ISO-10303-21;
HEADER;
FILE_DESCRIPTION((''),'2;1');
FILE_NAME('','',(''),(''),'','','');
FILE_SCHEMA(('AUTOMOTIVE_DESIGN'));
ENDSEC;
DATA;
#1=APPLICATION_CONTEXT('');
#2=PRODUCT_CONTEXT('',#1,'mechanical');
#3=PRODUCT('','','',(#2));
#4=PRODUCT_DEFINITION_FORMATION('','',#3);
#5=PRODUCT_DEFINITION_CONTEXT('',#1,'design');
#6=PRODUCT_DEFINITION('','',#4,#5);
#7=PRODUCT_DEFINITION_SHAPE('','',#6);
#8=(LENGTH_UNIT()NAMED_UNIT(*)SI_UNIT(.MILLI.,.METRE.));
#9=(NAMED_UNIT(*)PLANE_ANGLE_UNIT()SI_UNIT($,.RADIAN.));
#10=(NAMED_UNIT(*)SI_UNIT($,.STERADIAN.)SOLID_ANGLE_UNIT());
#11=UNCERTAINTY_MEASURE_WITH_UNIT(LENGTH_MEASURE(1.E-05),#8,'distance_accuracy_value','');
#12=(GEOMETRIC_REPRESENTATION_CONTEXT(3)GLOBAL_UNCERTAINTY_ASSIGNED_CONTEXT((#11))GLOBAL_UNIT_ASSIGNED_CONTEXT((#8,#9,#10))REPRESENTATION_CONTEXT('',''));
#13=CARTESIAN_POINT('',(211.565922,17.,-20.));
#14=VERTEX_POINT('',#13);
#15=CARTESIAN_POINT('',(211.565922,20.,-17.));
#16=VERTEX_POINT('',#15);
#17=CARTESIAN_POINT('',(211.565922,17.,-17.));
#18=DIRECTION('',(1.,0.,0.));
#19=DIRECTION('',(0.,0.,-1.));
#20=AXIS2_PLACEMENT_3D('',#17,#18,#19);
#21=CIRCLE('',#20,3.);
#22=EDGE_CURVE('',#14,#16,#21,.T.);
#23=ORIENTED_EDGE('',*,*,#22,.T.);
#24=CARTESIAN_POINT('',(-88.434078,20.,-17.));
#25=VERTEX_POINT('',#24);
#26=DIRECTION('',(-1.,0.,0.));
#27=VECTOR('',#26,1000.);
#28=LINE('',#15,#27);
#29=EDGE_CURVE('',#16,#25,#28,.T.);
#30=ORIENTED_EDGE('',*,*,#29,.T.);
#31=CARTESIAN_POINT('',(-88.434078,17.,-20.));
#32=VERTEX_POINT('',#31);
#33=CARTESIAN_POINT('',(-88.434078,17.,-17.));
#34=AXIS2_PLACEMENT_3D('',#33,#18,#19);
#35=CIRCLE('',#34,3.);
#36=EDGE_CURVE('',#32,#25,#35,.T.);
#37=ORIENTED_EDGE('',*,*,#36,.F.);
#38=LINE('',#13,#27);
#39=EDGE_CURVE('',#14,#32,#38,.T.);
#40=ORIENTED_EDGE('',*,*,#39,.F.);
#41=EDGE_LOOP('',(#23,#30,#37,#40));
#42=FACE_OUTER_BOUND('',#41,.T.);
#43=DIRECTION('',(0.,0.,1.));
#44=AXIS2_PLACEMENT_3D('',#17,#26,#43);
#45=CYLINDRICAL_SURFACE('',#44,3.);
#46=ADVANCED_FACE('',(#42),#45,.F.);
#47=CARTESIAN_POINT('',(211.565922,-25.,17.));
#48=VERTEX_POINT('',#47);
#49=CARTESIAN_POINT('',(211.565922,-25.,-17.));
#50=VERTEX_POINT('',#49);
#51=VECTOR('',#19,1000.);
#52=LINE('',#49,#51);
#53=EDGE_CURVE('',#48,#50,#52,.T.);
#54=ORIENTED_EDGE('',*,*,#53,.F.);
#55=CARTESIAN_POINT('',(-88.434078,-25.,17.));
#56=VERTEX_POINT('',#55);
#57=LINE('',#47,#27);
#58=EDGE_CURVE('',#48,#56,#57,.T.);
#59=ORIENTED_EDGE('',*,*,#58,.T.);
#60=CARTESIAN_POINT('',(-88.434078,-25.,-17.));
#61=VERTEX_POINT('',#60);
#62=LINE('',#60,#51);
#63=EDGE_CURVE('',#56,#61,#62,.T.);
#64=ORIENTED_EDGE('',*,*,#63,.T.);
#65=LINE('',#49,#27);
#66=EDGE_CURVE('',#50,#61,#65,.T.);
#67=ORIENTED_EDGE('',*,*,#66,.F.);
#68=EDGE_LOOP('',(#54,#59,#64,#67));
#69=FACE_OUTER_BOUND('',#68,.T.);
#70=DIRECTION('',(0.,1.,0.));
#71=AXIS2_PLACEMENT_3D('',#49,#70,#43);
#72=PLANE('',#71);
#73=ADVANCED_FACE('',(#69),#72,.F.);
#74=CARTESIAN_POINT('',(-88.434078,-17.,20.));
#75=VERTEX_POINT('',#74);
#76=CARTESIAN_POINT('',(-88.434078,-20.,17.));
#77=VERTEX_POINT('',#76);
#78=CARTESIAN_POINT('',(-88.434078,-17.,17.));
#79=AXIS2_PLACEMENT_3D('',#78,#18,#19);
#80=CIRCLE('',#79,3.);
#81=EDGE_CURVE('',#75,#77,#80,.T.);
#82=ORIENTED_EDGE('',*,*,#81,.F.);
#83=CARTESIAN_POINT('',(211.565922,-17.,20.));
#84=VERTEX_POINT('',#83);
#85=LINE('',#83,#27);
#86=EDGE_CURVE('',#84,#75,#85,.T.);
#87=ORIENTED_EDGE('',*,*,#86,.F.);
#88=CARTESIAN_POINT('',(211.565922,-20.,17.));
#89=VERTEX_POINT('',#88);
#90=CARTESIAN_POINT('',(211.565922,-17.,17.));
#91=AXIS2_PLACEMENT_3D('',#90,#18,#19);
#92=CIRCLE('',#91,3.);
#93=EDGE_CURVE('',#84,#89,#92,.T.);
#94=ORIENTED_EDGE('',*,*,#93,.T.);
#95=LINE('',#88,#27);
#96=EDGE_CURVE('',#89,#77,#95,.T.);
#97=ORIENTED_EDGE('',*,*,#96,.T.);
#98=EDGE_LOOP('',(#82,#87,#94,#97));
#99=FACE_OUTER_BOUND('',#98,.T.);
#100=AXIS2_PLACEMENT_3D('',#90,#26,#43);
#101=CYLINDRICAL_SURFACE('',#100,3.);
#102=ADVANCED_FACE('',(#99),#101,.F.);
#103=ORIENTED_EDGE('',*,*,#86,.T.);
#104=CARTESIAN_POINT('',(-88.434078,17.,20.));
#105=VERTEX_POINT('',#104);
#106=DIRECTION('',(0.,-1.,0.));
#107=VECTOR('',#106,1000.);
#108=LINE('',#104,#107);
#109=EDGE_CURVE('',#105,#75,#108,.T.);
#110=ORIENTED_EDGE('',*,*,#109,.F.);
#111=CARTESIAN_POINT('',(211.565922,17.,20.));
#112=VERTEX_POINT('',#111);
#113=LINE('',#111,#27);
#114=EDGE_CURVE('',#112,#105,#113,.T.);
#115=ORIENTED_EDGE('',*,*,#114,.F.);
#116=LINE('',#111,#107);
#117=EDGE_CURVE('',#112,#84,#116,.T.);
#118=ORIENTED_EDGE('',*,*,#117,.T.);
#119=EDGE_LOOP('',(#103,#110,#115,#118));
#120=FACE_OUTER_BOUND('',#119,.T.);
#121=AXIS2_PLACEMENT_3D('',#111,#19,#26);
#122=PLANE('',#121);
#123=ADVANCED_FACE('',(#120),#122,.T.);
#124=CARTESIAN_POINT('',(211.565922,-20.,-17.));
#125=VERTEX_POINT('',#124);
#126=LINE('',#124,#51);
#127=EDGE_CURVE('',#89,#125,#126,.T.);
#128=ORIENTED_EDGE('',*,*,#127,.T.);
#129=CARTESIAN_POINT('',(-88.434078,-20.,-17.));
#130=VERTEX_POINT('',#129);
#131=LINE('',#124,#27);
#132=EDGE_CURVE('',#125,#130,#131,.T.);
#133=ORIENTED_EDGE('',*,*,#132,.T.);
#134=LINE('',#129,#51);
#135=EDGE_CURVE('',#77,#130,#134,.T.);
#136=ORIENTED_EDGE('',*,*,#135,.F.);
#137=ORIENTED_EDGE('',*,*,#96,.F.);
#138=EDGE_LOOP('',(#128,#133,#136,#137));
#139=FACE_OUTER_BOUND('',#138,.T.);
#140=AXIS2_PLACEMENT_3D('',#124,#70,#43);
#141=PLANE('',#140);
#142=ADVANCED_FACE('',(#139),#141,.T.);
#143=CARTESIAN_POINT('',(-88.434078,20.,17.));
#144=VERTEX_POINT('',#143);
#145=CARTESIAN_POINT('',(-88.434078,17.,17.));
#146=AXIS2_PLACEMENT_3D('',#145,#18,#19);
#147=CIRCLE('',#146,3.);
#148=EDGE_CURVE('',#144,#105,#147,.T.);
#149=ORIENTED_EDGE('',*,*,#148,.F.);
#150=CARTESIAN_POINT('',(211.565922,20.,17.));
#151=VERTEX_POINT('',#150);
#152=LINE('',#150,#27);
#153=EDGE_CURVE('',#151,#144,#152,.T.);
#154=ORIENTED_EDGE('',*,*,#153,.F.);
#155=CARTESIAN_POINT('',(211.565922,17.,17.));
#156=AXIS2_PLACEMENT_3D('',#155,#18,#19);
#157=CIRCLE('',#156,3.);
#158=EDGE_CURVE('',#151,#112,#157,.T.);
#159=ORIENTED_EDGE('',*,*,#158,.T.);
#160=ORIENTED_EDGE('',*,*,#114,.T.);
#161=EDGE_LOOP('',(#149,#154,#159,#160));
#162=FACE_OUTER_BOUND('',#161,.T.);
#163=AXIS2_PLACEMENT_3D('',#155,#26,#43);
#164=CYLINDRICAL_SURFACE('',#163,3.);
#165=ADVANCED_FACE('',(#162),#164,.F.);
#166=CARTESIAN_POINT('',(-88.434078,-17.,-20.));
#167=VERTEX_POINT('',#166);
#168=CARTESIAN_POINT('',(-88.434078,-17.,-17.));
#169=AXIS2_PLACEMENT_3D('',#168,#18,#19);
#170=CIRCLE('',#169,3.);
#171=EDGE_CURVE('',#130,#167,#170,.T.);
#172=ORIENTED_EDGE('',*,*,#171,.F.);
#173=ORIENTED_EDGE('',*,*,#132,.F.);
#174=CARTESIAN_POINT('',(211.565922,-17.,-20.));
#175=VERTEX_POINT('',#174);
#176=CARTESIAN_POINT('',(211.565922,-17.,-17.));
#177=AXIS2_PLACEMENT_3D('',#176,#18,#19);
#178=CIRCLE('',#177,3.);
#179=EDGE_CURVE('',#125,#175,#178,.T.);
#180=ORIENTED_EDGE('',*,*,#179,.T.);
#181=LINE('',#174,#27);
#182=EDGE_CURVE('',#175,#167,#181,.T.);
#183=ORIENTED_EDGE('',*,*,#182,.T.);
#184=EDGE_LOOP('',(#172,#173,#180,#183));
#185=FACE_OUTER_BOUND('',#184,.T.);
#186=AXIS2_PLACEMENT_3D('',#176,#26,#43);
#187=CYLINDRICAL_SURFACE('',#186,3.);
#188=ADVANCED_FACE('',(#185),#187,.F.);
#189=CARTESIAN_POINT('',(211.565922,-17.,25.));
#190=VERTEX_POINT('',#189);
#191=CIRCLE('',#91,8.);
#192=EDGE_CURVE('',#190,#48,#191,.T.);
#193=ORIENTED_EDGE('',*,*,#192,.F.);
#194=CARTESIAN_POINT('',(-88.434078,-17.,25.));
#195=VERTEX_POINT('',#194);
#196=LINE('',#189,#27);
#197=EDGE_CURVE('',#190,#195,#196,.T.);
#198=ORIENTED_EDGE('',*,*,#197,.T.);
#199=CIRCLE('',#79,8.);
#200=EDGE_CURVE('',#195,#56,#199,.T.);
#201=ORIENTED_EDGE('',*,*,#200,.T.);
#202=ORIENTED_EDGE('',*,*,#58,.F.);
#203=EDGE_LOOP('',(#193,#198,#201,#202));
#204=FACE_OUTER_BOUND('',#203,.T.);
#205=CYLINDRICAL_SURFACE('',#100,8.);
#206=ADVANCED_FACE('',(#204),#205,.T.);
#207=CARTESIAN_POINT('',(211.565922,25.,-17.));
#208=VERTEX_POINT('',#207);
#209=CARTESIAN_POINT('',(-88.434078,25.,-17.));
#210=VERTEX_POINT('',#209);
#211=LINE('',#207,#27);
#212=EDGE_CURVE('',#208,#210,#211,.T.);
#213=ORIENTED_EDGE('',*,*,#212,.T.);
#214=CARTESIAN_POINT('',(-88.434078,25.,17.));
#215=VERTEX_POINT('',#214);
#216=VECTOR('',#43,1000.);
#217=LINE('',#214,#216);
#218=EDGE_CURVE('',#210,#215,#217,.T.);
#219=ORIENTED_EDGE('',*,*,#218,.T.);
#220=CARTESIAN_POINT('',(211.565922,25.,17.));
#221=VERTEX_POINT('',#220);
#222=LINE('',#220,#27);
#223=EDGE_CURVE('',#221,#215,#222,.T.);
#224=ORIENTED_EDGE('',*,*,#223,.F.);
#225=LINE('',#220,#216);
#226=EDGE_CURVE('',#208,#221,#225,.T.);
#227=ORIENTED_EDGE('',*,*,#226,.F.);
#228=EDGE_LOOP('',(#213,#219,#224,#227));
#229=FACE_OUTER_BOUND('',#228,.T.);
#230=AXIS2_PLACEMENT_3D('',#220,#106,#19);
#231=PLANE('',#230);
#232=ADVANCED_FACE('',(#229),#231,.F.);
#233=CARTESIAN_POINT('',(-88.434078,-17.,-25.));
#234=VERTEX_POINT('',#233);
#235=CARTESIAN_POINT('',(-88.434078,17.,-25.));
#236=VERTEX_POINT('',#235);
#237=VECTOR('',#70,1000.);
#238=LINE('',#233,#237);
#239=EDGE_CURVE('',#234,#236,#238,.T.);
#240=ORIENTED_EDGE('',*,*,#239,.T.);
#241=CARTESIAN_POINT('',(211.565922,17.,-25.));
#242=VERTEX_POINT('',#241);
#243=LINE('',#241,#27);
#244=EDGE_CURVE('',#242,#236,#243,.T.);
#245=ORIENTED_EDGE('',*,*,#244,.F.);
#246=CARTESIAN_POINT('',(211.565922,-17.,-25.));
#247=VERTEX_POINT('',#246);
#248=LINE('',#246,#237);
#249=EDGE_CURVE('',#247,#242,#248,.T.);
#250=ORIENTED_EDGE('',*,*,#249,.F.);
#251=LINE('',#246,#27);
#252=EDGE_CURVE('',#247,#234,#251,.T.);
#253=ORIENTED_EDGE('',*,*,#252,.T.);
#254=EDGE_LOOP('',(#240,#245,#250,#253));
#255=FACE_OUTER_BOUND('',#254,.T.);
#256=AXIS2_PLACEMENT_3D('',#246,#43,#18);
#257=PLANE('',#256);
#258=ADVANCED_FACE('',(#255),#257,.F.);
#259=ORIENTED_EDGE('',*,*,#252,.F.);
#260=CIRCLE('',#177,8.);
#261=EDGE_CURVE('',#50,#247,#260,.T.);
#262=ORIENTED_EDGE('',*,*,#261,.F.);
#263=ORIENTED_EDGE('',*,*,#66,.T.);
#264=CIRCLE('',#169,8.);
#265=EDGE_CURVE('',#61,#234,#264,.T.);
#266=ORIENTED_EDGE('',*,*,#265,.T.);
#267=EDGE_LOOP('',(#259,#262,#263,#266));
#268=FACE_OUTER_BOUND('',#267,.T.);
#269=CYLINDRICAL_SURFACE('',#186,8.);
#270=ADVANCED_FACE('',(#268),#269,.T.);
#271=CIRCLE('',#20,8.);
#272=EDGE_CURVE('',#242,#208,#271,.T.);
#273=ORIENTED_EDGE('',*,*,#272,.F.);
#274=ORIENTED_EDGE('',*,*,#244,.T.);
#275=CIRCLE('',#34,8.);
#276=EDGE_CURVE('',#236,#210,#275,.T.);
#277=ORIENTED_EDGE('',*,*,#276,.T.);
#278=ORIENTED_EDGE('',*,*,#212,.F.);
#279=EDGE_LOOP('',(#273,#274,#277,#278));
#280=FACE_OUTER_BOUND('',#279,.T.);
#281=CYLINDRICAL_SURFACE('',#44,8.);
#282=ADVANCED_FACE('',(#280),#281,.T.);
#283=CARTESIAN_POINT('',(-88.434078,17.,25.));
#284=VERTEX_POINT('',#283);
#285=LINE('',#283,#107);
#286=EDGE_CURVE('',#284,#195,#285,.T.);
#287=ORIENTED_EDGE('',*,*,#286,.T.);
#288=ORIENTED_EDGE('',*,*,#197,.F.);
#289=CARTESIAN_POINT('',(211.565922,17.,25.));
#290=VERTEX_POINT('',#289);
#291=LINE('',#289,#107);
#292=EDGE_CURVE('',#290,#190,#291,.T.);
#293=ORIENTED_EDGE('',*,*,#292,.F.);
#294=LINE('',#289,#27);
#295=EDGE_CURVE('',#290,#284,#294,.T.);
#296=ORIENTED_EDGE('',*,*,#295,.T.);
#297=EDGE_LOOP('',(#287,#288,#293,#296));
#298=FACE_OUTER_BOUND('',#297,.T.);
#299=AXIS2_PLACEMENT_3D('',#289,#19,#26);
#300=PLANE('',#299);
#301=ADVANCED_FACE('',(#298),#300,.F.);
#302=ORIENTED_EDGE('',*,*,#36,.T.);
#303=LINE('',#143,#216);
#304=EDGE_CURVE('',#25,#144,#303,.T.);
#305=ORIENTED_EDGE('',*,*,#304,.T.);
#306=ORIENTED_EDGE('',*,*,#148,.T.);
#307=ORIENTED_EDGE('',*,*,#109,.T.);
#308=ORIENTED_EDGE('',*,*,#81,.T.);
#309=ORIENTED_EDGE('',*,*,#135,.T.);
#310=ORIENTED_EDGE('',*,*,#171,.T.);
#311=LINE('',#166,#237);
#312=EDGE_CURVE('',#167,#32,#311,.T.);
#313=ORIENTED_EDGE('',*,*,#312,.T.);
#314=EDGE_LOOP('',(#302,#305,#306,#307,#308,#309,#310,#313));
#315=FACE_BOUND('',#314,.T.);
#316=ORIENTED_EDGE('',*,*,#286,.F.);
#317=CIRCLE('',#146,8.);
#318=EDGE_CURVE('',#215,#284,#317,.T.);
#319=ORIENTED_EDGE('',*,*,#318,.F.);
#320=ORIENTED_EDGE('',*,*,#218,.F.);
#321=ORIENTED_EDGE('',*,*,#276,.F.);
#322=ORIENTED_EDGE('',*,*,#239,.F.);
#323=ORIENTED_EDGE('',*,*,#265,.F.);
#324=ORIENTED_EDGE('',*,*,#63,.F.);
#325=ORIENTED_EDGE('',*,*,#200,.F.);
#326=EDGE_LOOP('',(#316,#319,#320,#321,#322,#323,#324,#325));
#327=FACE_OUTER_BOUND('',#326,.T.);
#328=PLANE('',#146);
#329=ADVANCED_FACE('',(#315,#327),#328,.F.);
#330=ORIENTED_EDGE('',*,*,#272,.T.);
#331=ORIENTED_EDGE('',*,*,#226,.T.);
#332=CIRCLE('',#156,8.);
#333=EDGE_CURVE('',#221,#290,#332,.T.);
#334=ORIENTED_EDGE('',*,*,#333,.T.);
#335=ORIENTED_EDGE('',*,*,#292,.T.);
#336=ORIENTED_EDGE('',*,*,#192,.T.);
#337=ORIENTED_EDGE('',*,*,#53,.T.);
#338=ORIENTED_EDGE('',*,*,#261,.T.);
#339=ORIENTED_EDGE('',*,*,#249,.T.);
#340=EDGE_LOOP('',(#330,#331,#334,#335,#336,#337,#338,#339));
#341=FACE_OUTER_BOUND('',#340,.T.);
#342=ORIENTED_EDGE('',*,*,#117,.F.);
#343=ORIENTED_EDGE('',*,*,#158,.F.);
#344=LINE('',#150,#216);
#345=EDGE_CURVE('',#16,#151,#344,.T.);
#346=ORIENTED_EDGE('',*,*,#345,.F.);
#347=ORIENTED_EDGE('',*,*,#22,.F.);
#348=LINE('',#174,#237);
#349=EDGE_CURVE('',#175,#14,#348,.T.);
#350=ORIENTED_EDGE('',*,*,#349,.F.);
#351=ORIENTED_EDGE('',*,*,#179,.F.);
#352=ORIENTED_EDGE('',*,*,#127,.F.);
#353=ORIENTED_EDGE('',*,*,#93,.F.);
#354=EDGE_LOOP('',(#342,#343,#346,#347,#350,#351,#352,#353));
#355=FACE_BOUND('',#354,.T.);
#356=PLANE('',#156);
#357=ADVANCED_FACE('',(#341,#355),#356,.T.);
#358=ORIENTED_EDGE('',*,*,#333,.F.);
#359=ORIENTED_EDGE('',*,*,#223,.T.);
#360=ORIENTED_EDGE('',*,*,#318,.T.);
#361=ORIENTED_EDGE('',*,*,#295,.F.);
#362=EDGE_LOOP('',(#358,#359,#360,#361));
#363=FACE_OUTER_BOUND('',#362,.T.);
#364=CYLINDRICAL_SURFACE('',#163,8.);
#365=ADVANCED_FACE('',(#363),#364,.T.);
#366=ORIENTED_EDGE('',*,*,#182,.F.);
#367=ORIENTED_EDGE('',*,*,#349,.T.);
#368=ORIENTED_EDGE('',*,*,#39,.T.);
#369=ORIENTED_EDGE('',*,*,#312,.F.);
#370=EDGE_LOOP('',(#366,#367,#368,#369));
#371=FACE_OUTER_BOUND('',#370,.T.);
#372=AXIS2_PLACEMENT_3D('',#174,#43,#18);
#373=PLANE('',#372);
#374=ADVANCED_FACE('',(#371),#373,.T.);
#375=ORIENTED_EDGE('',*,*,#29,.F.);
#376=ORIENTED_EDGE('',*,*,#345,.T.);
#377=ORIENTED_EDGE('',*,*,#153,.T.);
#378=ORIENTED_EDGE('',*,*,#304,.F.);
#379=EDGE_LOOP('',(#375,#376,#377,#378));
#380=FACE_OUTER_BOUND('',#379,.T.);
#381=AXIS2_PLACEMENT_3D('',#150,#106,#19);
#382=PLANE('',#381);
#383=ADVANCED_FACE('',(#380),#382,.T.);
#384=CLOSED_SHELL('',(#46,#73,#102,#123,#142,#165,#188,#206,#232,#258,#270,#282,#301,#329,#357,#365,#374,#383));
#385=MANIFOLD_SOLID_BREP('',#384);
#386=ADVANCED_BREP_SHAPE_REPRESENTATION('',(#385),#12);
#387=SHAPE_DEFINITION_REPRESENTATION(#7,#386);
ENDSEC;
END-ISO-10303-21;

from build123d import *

# Parameters (mm, degrees)
COLD_FORMED_SQUARE_HOLLOW_SECTION_GB_T_6_DEPTH = 300


with BuildPart() as part:
    # Sketch1 → Cold-formed square hollow section GB/T 6728-2002 50 X 50 X 4(1) (new body)
    with BuildSketch(Plane.YZ.offset(-88.434077868)):
        with BuildLine():
            Line((-17, -25), (17, -25))
            ThreePointArc((17, -25), (22.656854249, -22.656854249), (25, -17))
            Line((25, -17), (25, 17))
            ThreePointArc((25, 17), (22.656854249, 22.656854249), (17, 25))
            Line((17, 25), (-17, 25))
            ThreePointArc((-17, 25), (-22.656854249, 22.656854249), (-25, 17))
            Line((-25, 17), (-25, -17))
            ThreePointArc((-25, -17), (-22.656854249, -22.656854249), (-17, -25))
        make_face()
        with BuildLine():
            Line((-17, -20), (17, -20))
            ThreePointArc((17, -20), (19.121320344, -19.121320344), (20, -17))
            Line((20, -17), (20, 17))
            ThreePointArc((20, 17), (19.121320344, 19.121320344), (17, 20))
            Line((17, 20), (-17, 20))
            ThreePointArc((-17, 20), (-19.121320344, 19.121320344), (-20, 17))
            Line((-20, 17), (-20, -17))
            ThreePointArc((-20, -17), (-19.121320344, -19.121320344), (-17, -20))
        make_face(mode=Mode.SUBTRACT)
    extrude(amount=COLD_FORMED_SQUARE_HOLLOW_SECTION_GB_T_6_DEPTH)


solid = part.part
